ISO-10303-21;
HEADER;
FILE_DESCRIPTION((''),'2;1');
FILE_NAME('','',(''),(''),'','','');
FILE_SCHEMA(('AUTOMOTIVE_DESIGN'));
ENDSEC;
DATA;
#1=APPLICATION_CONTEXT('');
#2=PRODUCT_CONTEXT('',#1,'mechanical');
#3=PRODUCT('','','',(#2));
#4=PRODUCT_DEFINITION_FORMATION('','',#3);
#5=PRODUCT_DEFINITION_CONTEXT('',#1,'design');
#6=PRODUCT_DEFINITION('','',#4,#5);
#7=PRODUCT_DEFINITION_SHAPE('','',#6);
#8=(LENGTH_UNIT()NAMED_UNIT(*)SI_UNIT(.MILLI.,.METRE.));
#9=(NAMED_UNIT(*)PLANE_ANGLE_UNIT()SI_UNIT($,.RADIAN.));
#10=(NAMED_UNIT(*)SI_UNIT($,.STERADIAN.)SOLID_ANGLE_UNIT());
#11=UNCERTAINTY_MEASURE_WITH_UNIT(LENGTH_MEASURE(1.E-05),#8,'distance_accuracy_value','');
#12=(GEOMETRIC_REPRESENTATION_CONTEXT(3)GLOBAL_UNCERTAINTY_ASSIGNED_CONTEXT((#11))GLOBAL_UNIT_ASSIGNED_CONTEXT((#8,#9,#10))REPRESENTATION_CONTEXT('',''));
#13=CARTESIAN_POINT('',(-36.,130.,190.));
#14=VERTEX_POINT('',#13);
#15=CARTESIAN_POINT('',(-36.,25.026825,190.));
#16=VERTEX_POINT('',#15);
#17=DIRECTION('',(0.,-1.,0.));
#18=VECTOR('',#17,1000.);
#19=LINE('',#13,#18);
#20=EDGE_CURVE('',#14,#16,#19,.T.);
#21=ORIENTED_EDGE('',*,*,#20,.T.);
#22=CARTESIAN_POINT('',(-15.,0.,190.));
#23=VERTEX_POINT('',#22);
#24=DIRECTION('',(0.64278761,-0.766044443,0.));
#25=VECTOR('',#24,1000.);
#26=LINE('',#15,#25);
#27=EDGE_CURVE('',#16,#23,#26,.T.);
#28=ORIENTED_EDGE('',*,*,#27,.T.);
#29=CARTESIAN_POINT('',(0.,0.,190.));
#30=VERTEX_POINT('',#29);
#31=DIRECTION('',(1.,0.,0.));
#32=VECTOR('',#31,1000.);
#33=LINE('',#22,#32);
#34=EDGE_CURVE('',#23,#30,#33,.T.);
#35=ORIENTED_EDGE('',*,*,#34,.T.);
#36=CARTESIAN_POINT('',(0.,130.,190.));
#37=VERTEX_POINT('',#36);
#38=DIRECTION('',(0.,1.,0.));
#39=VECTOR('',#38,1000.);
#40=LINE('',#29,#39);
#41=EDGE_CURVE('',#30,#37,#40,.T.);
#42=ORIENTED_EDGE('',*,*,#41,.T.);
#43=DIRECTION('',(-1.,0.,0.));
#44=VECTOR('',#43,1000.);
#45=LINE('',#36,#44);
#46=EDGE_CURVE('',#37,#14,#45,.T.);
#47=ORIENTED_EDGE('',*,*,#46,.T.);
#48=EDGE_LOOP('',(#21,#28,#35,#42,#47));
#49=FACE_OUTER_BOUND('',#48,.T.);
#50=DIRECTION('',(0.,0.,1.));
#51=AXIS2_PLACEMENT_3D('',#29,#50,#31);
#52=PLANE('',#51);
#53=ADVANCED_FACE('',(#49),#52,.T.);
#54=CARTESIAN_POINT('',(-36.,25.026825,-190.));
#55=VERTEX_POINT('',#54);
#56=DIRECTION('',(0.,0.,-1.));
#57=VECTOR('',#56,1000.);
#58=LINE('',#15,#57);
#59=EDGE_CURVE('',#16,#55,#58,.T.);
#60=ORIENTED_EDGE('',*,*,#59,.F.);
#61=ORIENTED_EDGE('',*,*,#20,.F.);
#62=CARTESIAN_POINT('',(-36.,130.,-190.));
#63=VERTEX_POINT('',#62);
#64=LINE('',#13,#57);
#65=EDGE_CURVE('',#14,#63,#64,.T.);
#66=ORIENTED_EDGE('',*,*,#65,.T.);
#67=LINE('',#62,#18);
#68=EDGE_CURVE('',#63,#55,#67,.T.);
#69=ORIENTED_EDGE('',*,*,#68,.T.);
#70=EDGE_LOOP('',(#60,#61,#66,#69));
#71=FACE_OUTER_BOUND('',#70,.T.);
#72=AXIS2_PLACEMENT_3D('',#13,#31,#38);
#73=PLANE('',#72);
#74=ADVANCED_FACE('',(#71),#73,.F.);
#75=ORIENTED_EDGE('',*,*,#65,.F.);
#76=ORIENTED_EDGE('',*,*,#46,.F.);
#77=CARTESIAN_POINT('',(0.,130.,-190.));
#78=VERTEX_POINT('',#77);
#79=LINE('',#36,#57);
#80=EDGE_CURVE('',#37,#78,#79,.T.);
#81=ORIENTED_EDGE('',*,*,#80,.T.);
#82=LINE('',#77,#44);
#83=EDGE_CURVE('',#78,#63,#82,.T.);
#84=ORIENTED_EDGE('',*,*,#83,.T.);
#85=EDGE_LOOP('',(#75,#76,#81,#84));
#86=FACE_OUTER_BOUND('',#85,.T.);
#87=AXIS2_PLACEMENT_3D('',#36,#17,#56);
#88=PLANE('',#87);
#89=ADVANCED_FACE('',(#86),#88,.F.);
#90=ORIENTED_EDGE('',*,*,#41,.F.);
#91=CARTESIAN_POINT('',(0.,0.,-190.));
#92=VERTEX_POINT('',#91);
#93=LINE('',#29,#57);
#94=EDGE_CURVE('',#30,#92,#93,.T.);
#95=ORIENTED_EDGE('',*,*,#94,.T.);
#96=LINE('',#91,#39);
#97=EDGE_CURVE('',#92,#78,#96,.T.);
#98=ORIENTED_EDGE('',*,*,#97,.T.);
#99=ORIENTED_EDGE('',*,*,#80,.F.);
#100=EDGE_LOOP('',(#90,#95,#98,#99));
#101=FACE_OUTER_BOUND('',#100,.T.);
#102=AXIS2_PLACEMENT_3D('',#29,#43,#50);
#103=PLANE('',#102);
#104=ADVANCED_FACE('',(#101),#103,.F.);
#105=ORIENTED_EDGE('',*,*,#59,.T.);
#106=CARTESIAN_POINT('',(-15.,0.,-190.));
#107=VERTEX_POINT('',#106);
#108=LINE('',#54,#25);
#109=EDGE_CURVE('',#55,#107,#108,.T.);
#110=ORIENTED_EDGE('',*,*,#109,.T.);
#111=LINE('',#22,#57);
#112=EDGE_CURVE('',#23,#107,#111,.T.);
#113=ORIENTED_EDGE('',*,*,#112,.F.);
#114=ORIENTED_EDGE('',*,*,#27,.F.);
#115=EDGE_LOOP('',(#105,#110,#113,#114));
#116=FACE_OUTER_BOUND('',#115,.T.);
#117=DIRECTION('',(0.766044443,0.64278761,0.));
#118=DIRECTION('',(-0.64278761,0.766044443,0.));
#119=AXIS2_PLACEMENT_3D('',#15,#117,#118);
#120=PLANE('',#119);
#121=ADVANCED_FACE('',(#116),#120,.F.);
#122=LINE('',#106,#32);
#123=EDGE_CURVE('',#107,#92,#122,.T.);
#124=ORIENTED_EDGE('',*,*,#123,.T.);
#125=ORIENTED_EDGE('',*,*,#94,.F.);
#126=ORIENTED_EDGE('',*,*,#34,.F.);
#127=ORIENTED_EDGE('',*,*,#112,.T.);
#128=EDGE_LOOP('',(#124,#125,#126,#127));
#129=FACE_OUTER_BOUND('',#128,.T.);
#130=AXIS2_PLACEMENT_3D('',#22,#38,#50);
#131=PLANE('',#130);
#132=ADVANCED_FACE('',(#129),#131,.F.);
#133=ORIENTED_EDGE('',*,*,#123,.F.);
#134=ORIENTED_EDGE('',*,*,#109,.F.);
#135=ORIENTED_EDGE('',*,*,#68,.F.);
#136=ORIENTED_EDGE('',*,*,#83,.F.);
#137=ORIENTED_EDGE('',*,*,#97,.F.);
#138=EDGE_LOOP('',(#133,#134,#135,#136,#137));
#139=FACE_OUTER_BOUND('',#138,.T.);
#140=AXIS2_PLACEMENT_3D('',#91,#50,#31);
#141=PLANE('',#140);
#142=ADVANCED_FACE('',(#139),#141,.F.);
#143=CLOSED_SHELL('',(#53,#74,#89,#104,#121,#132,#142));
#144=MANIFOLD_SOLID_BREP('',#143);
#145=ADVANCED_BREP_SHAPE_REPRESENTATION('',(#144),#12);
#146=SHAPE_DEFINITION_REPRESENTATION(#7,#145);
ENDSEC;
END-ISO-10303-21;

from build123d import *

# Parameters (mm, degrees)
BOSS_EXTRUDE1_DEPTH = 190


with BuildPart() as part:
    # Sketch1 → Boss-Extrude1 (new, symmetric)
    with BuildSketch(Plane.XY):
        Polygon((0, 0), (0, 130), (-36, 130), (-36, 25.026825444), (-15, 0), align=None)
    extrude(amount=BOSS_EXTRUDE1_DEPTH, both=True)


solid = part.part
